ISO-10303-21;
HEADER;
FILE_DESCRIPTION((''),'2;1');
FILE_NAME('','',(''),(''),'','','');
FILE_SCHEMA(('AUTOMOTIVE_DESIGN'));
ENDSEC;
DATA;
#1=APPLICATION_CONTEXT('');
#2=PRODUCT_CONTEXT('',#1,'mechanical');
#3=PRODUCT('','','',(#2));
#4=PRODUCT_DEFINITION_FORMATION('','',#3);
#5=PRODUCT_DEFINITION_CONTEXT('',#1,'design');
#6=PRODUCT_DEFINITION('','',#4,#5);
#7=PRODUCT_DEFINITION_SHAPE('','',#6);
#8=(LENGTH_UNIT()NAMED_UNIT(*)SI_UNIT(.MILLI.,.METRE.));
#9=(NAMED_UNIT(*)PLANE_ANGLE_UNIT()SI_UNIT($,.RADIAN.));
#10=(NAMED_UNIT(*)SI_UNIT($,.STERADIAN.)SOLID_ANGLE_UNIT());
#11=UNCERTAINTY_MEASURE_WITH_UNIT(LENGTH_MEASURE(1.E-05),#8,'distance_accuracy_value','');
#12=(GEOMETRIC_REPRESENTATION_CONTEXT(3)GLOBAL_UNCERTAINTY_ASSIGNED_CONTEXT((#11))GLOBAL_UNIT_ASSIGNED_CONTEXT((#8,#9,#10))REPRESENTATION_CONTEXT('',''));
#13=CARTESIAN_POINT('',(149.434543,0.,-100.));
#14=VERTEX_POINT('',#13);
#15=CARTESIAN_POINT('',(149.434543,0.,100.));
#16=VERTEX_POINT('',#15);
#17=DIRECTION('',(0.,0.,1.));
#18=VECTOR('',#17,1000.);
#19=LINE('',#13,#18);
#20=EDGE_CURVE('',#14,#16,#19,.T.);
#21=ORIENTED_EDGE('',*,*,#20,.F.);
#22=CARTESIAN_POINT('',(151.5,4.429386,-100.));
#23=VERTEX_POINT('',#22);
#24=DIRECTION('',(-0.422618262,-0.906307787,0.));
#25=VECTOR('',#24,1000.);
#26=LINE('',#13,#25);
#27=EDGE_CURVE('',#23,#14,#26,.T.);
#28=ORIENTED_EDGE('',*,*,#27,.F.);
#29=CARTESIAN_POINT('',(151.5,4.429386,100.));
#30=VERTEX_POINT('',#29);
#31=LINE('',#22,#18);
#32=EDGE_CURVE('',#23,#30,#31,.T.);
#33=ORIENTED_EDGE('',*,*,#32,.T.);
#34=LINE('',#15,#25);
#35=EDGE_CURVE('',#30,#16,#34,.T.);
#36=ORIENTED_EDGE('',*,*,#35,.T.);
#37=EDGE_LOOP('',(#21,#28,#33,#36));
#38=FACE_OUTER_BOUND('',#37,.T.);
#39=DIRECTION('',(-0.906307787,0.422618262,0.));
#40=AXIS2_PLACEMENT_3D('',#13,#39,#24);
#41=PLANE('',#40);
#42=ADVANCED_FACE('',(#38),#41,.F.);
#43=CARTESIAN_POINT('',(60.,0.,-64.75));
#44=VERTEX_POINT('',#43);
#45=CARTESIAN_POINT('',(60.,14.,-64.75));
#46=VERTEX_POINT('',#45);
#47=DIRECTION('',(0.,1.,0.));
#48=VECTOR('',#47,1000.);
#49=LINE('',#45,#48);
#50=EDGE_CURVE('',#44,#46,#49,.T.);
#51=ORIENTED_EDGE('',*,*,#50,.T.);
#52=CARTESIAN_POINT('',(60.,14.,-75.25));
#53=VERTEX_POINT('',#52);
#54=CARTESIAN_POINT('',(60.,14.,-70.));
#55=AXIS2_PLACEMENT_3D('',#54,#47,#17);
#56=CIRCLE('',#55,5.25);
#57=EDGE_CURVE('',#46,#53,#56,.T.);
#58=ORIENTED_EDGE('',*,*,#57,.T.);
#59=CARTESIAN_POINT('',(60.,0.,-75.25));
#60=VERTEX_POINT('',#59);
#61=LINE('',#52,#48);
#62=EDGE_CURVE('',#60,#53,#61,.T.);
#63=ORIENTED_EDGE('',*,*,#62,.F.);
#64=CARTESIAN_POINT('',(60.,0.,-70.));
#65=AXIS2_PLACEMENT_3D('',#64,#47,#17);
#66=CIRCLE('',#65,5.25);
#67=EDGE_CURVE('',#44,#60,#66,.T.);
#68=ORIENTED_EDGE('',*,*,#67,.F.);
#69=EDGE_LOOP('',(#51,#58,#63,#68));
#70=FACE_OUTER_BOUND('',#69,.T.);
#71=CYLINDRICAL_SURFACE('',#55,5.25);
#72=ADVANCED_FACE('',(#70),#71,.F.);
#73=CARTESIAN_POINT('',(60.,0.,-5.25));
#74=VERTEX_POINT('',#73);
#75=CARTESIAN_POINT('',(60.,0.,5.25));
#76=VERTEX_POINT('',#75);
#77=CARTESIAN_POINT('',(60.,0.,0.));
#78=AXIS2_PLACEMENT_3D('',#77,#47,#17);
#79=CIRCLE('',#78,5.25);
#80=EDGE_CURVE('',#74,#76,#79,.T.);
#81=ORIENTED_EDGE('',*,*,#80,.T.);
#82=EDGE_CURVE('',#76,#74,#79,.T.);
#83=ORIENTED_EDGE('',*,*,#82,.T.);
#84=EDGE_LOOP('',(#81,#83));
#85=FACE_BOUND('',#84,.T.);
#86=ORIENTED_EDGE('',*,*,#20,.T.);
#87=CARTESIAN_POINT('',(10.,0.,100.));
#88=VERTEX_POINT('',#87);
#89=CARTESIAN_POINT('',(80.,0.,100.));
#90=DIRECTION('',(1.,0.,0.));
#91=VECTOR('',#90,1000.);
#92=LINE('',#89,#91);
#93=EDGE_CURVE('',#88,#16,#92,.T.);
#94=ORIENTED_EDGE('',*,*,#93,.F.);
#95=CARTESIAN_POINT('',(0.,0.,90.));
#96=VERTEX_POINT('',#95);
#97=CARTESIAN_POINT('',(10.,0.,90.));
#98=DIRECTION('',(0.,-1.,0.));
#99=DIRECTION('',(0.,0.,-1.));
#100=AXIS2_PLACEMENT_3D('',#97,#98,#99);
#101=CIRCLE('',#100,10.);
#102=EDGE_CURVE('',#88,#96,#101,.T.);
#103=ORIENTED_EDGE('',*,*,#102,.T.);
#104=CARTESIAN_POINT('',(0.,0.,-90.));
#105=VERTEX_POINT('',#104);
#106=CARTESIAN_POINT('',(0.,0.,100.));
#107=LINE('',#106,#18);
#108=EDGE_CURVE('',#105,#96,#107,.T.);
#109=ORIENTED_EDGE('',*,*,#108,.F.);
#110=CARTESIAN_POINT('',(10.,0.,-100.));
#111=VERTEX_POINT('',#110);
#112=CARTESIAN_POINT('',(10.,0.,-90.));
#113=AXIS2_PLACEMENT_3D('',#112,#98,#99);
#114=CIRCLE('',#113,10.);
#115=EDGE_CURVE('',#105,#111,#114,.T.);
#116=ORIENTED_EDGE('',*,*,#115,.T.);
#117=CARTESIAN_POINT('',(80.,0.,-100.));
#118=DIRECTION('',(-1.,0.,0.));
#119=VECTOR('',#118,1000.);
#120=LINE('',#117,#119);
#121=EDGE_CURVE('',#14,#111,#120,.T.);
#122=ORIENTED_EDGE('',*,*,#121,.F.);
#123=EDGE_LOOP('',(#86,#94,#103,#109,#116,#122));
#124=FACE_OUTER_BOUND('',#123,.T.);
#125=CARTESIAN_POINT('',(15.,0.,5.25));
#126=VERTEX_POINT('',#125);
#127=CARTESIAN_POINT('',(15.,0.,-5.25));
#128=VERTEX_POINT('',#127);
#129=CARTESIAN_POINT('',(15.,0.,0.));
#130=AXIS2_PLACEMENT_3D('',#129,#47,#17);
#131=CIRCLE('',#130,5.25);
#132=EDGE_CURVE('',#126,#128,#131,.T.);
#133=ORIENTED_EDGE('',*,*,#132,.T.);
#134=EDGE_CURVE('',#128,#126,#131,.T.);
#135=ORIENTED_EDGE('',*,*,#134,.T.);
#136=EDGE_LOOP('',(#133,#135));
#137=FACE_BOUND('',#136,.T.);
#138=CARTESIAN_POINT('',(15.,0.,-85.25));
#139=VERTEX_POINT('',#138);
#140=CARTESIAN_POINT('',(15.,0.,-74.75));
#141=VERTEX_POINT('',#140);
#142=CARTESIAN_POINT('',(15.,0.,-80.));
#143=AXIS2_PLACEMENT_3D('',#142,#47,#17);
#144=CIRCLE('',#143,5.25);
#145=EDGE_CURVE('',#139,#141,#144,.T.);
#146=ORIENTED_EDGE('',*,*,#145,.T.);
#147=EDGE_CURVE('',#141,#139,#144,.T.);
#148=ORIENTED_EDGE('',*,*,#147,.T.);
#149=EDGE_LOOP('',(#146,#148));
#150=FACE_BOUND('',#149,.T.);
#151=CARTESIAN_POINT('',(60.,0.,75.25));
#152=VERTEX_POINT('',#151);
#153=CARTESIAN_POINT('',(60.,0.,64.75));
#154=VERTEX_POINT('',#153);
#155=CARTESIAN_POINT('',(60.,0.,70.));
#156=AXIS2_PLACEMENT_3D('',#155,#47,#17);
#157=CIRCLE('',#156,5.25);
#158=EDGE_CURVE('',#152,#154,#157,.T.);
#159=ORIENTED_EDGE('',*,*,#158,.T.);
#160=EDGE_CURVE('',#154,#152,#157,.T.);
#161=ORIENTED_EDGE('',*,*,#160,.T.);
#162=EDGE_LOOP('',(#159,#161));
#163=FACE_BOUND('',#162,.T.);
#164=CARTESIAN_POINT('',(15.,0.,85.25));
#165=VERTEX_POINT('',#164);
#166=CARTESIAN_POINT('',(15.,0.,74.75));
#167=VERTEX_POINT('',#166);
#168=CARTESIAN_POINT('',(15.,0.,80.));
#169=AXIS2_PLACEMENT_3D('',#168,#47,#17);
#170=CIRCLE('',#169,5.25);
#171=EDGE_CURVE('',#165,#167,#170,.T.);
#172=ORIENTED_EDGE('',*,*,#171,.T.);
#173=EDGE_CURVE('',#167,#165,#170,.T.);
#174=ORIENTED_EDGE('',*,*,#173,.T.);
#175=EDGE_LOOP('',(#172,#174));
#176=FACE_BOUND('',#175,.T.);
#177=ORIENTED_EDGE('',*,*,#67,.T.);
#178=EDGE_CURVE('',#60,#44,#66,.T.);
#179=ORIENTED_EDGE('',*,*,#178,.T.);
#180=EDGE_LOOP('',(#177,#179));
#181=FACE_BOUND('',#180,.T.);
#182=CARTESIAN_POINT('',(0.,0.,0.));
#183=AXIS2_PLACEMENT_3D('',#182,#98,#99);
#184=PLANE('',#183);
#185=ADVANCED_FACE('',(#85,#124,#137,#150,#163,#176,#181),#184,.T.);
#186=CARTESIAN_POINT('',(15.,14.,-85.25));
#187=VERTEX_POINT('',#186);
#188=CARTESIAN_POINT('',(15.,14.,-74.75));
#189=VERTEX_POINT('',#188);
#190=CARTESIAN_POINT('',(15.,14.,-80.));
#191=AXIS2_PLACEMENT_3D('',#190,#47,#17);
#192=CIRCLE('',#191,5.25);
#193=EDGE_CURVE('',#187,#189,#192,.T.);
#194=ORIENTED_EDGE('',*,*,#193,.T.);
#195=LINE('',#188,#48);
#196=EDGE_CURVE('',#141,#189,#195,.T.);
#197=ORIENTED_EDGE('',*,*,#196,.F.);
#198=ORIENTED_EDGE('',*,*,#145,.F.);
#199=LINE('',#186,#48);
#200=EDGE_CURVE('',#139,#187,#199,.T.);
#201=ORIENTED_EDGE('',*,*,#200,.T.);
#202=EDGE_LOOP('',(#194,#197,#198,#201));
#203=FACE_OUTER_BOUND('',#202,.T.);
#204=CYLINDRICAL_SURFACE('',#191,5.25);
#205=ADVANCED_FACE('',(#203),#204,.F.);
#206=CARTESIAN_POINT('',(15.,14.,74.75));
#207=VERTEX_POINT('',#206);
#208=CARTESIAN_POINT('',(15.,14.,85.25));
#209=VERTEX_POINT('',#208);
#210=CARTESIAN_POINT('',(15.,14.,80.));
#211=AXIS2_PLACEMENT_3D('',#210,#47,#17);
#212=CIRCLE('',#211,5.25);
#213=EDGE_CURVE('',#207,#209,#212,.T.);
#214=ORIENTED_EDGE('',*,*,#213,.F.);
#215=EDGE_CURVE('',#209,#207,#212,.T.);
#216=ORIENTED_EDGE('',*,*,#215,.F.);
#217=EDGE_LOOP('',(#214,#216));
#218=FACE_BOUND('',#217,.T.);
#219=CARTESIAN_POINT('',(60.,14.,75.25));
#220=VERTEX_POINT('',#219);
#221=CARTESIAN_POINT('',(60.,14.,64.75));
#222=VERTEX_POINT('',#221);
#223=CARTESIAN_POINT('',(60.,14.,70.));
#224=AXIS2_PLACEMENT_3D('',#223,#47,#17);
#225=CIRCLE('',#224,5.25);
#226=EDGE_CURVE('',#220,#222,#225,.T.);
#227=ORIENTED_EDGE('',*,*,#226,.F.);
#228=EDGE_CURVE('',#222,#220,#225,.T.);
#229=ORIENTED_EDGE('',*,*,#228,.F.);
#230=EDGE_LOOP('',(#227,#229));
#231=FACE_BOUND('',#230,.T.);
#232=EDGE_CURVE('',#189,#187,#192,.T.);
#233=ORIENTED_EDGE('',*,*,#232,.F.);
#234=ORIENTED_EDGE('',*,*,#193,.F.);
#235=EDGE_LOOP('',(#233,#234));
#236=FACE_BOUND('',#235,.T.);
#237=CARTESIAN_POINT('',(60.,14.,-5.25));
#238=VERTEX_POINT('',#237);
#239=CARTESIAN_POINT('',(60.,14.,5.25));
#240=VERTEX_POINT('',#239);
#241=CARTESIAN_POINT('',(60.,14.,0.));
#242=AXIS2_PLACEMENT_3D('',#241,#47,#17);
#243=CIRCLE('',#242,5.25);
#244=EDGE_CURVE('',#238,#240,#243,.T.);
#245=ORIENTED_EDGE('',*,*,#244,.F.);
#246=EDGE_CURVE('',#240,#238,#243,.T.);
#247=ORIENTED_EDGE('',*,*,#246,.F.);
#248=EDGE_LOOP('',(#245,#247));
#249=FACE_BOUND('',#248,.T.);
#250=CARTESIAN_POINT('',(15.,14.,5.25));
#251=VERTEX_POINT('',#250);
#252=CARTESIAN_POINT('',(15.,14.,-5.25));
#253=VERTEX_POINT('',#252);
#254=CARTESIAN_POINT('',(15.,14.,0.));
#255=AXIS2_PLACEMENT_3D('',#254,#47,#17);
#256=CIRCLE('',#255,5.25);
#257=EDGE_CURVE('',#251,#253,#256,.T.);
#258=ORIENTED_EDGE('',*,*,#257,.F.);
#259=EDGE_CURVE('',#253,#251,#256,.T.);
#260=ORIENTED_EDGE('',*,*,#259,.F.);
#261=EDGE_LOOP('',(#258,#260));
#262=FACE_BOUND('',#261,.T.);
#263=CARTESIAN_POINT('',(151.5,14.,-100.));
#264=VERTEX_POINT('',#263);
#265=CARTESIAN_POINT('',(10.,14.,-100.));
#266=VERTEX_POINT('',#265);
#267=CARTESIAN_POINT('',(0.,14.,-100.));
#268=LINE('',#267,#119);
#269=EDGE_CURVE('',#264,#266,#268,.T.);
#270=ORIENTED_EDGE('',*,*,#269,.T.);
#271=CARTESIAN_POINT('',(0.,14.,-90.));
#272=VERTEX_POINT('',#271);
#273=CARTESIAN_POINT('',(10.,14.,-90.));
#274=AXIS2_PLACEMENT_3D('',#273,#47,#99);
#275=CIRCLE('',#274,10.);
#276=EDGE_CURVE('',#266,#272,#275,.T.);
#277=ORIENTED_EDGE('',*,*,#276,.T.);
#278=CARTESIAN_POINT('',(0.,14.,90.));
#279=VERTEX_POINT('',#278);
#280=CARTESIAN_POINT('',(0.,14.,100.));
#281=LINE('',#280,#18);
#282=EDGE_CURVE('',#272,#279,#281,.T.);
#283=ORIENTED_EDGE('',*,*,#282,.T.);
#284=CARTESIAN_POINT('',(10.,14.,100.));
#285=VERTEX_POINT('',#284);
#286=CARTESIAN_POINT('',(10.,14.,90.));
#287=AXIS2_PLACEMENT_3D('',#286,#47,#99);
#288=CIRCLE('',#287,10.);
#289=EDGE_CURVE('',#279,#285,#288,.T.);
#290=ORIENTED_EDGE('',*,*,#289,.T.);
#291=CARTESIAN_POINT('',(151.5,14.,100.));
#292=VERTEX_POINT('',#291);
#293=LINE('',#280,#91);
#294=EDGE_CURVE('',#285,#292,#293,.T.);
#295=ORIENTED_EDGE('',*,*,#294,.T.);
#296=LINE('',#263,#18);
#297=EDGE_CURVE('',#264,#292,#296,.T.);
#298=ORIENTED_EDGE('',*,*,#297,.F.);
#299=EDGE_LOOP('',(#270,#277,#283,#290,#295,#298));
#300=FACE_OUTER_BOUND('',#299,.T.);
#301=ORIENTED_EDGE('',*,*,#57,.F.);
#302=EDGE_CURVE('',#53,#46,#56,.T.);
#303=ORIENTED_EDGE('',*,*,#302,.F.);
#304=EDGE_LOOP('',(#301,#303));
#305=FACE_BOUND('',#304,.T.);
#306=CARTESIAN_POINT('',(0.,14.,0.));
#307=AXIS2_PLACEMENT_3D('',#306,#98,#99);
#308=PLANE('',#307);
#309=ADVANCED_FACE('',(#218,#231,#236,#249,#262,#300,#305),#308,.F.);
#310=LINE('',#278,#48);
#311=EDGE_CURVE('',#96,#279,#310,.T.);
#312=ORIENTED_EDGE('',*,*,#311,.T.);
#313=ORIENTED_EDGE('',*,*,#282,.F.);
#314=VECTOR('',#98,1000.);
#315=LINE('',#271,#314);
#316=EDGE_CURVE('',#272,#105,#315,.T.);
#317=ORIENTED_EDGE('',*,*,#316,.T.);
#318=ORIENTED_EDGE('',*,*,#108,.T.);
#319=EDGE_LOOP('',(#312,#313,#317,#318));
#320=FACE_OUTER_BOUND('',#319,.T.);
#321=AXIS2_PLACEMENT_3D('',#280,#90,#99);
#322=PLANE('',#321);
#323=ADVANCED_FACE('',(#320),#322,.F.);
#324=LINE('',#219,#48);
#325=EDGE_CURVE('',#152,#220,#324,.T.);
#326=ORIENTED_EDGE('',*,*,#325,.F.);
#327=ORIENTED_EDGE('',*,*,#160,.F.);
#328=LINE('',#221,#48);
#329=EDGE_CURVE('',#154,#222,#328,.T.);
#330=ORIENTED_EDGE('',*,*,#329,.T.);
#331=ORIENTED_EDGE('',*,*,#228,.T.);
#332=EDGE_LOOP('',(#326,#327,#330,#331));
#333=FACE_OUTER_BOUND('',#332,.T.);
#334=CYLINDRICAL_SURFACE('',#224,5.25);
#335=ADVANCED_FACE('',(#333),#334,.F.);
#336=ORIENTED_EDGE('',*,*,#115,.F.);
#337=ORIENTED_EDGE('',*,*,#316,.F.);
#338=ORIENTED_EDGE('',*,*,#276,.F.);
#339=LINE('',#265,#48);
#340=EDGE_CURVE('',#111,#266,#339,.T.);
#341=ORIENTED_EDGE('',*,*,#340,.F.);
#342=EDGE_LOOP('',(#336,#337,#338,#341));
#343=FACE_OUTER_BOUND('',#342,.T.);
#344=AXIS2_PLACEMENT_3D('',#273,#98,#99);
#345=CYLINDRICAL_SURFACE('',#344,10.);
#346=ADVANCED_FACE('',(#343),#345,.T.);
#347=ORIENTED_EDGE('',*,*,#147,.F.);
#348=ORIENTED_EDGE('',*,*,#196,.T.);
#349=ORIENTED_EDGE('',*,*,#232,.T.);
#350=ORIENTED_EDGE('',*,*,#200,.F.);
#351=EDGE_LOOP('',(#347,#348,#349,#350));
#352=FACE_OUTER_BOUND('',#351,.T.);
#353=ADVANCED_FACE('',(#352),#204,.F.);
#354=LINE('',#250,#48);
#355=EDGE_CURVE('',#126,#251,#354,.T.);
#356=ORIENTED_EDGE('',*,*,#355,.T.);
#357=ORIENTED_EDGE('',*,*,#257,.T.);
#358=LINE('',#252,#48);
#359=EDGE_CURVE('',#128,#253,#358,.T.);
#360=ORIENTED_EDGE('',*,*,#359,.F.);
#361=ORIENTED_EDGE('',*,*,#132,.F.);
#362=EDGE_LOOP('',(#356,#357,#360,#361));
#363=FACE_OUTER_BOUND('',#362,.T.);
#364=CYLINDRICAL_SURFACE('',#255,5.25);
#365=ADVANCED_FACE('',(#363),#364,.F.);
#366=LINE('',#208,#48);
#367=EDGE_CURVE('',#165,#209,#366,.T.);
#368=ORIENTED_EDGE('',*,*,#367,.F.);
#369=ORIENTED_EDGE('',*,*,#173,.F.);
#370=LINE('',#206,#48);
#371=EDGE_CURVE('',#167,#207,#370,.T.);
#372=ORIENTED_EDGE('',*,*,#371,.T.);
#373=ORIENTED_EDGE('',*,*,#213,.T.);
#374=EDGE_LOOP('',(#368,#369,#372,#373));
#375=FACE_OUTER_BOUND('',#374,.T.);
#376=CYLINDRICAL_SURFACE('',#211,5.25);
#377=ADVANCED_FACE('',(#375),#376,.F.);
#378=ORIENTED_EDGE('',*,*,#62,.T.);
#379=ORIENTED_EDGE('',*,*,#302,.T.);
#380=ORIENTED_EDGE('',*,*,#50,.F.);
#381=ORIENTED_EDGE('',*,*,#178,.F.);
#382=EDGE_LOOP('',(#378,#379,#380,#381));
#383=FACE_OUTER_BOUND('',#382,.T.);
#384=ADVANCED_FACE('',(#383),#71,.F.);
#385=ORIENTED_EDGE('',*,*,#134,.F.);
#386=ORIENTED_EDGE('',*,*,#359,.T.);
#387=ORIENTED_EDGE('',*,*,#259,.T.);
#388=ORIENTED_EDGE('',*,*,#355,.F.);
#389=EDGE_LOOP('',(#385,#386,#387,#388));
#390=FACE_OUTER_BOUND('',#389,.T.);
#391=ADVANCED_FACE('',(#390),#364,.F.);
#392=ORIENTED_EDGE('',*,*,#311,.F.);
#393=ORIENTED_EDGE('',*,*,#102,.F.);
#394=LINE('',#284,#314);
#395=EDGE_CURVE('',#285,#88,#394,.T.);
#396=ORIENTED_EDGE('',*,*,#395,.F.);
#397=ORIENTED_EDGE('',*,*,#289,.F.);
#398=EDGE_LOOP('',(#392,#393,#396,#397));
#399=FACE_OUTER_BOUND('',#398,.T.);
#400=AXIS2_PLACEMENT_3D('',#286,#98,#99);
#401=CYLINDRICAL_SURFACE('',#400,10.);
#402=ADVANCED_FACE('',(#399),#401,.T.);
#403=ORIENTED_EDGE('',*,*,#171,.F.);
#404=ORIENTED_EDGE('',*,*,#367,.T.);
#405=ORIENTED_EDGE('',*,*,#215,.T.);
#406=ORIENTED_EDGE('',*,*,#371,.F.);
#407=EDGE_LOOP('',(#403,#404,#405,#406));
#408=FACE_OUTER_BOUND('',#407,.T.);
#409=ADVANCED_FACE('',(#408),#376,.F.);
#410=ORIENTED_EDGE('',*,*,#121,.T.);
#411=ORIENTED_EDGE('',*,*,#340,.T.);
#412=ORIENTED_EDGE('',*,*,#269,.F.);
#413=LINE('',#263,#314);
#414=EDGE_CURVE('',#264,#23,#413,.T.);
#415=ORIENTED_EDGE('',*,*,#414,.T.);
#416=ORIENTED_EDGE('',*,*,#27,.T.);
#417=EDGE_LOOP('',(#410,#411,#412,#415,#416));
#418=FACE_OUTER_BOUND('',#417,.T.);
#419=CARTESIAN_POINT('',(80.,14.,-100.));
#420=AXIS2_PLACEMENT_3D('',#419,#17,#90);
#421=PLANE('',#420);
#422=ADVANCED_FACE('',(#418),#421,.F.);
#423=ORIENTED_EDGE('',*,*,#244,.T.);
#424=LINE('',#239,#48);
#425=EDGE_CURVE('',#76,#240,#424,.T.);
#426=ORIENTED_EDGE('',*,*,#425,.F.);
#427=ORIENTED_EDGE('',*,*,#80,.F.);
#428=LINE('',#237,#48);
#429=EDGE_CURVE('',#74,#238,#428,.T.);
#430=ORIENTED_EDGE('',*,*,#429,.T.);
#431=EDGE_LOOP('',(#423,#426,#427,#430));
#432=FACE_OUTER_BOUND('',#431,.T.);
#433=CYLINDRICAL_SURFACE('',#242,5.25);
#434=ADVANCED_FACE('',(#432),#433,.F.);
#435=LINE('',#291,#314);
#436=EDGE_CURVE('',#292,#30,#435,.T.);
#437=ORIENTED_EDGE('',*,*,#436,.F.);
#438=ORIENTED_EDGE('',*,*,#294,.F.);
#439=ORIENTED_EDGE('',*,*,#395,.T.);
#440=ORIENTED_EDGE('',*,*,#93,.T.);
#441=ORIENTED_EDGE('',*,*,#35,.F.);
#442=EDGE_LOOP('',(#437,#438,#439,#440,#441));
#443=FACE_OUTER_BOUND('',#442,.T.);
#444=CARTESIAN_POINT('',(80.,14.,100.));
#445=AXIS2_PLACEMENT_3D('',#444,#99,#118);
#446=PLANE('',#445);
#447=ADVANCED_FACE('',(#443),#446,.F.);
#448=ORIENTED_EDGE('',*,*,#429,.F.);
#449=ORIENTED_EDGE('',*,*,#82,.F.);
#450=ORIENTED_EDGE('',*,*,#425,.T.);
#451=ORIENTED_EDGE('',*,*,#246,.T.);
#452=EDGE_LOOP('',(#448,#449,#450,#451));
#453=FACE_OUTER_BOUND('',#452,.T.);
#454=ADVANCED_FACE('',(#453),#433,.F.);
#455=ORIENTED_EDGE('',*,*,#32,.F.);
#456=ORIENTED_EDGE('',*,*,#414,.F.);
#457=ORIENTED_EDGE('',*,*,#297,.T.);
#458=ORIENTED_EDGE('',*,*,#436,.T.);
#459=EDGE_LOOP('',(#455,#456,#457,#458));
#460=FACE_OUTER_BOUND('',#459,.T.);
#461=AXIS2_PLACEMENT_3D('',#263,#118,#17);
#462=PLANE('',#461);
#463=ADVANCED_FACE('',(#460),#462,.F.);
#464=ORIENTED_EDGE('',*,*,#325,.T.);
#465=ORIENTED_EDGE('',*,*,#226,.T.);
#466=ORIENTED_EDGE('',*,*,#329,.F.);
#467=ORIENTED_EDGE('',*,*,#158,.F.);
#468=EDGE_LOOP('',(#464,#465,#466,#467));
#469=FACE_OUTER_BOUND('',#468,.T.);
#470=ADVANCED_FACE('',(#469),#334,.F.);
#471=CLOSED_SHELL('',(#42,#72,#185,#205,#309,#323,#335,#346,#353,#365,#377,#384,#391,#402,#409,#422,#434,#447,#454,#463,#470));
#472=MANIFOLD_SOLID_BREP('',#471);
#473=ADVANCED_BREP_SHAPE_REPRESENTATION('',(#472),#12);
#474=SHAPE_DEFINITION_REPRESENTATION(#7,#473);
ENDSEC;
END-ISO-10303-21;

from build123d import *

# Parameters (mm, degrees)
BOSS_EXTRUDE1_DEPTH          = 14
FILLET1_R                    = 10
F_10_5_10_5_DIAMETER_HOLE1_D = 10.5
F_10_5_10_5_DIAMETER_HOLE2_D = 10.5
CUT_EXTRUDE1_DEPTH           = 257.507309837
SKETCH8_W                    = 4.462850671
SKETCH8_H                    = 15.00402921
CUT_EXTRUDE2_DEPTH           = 255.008682508


with BuildPart() as part:
    # Sketch1 → Boss-Extrude1 (new body)
    with BuildSketch(Plane(origin=(0, 0, 0), x_dir=(1, 0, 0), z_dir=(0, 1, 0))):
        Polygon((0, -100), (0, 100), (80, 100), (160, 100), (160, -100), (80, -100), align=None)
    extrude(amount=BOSS_EXTRUDE1_DEPTH)

    # Fillet1
    fillet1_edges = [part.edges().sort_by_distance(p)[0] for p in [
        (0, 7, 100),
        (0, 7, -100),
    ]]
    fillet(fillet1_edges, radius=FILLET1_R)

    # Ø10.5 (10.5) Diameter Hole1 (through all)
    with Locations(Plane(origin=(0, 14, 0), x_dir=(1, 0, 0), z_dir=(0, 1, 0))):
        with Locations((60, 70), (60, -70), (60, 0)):
            Hole(F_10_5_10_5_DIAMETER_HOLE1_D / 2)

    # Ø10.5 (10.5) Diameter Hole2 (through all)
    with Locations(Plane(origin=(0, 14, 0), x_dir=(1, 0, 0), z_dir=(0, 1, 0))):
        with Locations((15, 80), (15, -80), (15, 0)):
            Hole(F_10_5_10_5_DIAMETER_HOLE2_D / 2)

    # Sketch7 → Cut-Extrude1 (cut, through all)
    with BuildSketch(Plane.XY.offset(100)):
        Polygon((149.434543456, 0), (160, 22.657694676), (160, 0), align=None)
    extrude(amount=-CUT_EXTRUDE1_DEPTH, mode=Mode.SUBTRACT)

    # Sketch8 → Cut-Extrude2 (cut, through all)
    with BuildSketch(Plane.XY.offset(100)):
        with Locations((153.731425336, 6.497985395)):
            Rectangle(SKETCH8_W, SKETCH8_H)
    extrude(amount=-CUT_EXTRUDE2_DEPTH, mode=Mode.SUBTRACT)


solid = part.part
